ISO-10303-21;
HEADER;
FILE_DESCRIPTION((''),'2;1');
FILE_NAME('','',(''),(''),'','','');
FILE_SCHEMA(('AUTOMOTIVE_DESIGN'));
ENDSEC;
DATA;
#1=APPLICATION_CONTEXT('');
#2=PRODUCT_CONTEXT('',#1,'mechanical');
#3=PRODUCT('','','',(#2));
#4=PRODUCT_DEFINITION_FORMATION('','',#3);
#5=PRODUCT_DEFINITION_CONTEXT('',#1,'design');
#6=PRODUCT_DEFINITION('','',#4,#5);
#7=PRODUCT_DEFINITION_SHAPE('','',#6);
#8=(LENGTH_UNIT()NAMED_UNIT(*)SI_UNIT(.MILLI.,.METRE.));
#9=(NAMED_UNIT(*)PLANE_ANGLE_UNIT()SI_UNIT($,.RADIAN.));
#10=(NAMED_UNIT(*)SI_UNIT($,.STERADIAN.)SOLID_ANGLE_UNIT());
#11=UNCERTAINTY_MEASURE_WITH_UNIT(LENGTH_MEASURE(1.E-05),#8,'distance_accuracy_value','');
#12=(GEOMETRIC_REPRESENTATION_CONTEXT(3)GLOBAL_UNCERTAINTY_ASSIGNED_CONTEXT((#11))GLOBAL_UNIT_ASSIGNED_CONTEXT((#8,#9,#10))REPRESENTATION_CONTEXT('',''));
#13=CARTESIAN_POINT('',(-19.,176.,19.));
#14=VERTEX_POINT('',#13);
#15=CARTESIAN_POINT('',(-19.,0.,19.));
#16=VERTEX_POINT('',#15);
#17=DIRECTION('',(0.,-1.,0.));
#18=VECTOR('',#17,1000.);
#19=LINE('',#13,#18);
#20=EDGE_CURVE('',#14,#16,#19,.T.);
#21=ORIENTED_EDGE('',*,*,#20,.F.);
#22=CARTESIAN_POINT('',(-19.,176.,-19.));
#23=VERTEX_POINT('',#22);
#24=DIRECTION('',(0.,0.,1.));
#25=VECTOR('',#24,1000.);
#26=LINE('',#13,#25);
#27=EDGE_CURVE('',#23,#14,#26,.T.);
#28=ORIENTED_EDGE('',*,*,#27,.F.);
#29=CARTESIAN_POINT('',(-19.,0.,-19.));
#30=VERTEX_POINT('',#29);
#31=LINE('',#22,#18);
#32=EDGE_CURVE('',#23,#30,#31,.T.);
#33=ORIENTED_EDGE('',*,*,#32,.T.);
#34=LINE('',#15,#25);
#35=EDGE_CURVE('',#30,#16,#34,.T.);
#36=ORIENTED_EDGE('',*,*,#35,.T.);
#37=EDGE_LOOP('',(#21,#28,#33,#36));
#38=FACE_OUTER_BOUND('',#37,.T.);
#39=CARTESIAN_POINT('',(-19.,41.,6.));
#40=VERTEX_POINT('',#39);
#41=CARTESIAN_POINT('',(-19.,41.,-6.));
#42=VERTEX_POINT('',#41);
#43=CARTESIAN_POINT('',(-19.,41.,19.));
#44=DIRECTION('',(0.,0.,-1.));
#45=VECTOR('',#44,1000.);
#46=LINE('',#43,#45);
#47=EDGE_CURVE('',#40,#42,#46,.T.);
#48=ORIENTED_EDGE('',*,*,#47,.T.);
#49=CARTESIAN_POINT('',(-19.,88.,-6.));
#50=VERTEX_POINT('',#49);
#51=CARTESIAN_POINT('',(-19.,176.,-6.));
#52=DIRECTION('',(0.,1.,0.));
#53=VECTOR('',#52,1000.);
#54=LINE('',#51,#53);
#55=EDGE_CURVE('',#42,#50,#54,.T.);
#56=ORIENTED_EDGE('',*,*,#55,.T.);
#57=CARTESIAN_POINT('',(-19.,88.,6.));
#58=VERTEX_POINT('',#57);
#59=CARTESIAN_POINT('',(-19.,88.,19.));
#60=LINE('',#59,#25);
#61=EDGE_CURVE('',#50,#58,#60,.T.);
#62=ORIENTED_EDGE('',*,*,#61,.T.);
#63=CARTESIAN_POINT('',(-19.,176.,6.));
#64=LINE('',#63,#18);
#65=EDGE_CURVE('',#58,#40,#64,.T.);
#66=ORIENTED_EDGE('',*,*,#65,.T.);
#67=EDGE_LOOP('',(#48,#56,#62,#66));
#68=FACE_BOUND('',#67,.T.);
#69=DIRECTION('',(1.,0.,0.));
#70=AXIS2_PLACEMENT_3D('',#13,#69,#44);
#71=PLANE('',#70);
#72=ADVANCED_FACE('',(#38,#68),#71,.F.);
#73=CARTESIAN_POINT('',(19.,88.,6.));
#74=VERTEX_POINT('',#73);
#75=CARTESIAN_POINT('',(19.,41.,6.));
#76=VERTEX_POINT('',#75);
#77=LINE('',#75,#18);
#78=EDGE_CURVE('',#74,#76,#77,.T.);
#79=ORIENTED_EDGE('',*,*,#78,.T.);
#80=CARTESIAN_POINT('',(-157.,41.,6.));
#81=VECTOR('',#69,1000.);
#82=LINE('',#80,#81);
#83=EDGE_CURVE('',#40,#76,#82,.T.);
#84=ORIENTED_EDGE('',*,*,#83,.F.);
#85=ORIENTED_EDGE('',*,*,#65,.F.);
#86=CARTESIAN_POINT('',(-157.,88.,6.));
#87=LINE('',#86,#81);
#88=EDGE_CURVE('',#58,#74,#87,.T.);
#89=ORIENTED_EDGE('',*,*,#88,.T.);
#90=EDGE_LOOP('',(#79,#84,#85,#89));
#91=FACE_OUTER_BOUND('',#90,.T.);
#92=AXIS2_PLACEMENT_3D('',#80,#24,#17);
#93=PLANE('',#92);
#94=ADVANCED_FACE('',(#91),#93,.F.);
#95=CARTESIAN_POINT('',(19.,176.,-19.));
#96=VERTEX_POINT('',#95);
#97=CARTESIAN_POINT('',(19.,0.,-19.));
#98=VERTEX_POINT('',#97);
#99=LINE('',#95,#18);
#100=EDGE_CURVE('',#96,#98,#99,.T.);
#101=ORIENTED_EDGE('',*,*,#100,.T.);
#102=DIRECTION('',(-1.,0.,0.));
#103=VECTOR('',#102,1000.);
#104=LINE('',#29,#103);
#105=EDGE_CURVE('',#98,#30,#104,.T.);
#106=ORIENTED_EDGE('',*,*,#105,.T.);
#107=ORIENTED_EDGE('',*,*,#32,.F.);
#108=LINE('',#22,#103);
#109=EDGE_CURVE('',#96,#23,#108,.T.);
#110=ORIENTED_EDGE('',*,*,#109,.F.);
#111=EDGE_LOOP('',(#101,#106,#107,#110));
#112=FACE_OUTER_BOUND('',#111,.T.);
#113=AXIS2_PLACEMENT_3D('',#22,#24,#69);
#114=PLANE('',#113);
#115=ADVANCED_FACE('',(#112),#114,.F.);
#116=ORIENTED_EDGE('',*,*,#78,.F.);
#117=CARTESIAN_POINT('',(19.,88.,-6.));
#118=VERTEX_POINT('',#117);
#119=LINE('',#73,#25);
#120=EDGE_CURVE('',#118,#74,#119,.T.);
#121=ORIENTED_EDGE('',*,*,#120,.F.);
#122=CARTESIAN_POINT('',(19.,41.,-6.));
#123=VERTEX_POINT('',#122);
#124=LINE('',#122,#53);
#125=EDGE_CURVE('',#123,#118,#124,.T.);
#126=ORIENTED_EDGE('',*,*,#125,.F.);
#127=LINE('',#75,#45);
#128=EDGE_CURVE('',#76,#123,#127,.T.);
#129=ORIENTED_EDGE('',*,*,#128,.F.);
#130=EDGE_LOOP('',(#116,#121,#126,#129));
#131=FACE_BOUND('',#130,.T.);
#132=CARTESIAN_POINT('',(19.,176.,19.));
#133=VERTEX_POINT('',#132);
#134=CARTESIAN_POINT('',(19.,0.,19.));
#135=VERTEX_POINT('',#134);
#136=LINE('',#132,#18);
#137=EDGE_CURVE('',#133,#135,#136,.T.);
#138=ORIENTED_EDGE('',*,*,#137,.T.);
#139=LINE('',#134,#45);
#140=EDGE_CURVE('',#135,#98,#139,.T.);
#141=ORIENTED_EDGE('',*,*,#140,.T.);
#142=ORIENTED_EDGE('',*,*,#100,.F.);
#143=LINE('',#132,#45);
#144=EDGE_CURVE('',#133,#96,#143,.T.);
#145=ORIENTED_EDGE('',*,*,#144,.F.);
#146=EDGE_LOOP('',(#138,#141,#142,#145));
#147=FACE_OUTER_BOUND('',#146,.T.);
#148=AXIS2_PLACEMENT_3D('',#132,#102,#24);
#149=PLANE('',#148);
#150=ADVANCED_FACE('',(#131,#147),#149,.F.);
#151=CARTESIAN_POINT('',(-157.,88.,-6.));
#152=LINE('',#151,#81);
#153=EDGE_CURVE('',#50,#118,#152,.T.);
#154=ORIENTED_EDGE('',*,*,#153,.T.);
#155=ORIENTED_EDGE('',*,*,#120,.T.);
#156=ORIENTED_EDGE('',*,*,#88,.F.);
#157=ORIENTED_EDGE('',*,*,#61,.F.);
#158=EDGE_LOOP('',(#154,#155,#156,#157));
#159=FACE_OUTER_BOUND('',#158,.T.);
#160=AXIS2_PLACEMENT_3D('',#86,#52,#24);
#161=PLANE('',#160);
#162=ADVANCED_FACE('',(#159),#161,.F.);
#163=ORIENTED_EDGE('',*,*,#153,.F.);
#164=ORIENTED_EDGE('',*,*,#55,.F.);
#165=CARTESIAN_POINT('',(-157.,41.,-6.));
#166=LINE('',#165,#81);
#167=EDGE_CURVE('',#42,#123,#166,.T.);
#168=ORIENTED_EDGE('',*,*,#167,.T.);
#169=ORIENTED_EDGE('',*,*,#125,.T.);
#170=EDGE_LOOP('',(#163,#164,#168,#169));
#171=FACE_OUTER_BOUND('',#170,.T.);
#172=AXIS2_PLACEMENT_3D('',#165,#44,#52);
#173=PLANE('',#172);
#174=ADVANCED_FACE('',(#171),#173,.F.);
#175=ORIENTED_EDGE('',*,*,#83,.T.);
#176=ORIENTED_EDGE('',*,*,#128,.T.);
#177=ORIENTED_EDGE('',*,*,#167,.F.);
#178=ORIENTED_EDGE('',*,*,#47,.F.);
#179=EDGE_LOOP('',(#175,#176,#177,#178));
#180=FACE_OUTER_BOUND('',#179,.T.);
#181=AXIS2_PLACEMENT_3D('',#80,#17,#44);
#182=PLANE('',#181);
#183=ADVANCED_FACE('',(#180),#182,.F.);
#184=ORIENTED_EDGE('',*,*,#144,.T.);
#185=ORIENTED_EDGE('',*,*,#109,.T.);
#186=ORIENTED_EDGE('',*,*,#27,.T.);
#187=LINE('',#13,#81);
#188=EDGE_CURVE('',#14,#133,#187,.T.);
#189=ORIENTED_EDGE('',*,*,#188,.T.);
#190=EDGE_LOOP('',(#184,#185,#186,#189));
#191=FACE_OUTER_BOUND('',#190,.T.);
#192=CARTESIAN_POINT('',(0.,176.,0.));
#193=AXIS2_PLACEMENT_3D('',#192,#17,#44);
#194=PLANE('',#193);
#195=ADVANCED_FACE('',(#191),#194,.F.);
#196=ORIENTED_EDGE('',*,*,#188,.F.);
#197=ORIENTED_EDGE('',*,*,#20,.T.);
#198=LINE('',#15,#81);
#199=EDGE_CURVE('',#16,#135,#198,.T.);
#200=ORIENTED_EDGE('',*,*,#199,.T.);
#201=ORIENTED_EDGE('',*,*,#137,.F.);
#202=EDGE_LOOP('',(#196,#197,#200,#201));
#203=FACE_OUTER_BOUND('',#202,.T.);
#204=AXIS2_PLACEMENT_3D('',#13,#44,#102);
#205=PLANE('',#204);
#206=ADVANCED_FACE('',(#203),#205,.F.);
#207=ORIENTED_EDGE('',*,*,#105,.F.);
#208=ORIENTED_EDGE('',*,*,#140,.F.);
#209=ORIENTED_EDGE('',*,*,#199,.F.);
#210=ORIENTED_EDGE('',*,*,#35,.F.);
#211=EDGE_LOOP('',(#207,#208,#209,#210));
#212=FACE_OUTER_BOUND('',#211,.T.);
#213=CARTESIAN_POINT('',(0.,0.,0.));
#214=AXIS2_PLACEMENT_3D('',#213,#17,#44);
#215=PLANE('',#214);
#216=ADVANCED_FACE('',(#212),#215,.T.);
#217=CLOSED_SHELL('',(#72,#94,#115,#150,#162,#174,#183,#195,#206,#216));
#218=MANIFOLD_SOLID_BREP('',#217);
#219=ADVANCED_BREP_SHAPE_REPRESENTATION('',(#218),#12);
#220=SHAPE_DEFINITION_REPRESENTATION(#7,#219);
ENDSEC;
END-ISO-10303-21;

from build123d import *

# Parameters (mm, degrees)
ROD_SECTION_SKETCH_38X38_W = 38
ROD_SECTION_SKETCH_38X38_H = 38
SQUARE_ROD_38X38X176_DEPTH = 176
SLOT_PROFILE_SKETCH_W      = 12
SLOT_PROFILE_SKETCH_H      = 47
THROUGH_SLOT_47X12_DEPTH   = 176


with BuildPart() as part:
    # Rod Section Sketch 38x38 → Square Rod 38x38x176 (new body)
    with BuildSketch(Plane(origin=(0, 0, 0), x_dir=(1, 0, 0), z_dir=(0, 1, 0))):
        Rectangle(ROD_SECTION_SKETCH_38X38_W, ROD_SECTION_SKETCH_38X38_H)
    extrude(amount=SQUARE_ROD_38X38X176_DEPTH)

    # Slot Profile Sketch → Through Slot 47x12 (cut)
    with BuildSketch(Plane(origin=(19, 0, 0), x_dir=(0, 0, -1), z_dir=(1, 0, 0))):
        with Locations((0, 64.5)):
            Rectangle(SLOT_PROFILE_SKETCH_W, SLOT_PROFILE_SKETCH_H)
    extrude(amount=-THROUGH_SLOT_47X12_DEPTH, mode=Mode.SUBTRACT)


solid = part.part
